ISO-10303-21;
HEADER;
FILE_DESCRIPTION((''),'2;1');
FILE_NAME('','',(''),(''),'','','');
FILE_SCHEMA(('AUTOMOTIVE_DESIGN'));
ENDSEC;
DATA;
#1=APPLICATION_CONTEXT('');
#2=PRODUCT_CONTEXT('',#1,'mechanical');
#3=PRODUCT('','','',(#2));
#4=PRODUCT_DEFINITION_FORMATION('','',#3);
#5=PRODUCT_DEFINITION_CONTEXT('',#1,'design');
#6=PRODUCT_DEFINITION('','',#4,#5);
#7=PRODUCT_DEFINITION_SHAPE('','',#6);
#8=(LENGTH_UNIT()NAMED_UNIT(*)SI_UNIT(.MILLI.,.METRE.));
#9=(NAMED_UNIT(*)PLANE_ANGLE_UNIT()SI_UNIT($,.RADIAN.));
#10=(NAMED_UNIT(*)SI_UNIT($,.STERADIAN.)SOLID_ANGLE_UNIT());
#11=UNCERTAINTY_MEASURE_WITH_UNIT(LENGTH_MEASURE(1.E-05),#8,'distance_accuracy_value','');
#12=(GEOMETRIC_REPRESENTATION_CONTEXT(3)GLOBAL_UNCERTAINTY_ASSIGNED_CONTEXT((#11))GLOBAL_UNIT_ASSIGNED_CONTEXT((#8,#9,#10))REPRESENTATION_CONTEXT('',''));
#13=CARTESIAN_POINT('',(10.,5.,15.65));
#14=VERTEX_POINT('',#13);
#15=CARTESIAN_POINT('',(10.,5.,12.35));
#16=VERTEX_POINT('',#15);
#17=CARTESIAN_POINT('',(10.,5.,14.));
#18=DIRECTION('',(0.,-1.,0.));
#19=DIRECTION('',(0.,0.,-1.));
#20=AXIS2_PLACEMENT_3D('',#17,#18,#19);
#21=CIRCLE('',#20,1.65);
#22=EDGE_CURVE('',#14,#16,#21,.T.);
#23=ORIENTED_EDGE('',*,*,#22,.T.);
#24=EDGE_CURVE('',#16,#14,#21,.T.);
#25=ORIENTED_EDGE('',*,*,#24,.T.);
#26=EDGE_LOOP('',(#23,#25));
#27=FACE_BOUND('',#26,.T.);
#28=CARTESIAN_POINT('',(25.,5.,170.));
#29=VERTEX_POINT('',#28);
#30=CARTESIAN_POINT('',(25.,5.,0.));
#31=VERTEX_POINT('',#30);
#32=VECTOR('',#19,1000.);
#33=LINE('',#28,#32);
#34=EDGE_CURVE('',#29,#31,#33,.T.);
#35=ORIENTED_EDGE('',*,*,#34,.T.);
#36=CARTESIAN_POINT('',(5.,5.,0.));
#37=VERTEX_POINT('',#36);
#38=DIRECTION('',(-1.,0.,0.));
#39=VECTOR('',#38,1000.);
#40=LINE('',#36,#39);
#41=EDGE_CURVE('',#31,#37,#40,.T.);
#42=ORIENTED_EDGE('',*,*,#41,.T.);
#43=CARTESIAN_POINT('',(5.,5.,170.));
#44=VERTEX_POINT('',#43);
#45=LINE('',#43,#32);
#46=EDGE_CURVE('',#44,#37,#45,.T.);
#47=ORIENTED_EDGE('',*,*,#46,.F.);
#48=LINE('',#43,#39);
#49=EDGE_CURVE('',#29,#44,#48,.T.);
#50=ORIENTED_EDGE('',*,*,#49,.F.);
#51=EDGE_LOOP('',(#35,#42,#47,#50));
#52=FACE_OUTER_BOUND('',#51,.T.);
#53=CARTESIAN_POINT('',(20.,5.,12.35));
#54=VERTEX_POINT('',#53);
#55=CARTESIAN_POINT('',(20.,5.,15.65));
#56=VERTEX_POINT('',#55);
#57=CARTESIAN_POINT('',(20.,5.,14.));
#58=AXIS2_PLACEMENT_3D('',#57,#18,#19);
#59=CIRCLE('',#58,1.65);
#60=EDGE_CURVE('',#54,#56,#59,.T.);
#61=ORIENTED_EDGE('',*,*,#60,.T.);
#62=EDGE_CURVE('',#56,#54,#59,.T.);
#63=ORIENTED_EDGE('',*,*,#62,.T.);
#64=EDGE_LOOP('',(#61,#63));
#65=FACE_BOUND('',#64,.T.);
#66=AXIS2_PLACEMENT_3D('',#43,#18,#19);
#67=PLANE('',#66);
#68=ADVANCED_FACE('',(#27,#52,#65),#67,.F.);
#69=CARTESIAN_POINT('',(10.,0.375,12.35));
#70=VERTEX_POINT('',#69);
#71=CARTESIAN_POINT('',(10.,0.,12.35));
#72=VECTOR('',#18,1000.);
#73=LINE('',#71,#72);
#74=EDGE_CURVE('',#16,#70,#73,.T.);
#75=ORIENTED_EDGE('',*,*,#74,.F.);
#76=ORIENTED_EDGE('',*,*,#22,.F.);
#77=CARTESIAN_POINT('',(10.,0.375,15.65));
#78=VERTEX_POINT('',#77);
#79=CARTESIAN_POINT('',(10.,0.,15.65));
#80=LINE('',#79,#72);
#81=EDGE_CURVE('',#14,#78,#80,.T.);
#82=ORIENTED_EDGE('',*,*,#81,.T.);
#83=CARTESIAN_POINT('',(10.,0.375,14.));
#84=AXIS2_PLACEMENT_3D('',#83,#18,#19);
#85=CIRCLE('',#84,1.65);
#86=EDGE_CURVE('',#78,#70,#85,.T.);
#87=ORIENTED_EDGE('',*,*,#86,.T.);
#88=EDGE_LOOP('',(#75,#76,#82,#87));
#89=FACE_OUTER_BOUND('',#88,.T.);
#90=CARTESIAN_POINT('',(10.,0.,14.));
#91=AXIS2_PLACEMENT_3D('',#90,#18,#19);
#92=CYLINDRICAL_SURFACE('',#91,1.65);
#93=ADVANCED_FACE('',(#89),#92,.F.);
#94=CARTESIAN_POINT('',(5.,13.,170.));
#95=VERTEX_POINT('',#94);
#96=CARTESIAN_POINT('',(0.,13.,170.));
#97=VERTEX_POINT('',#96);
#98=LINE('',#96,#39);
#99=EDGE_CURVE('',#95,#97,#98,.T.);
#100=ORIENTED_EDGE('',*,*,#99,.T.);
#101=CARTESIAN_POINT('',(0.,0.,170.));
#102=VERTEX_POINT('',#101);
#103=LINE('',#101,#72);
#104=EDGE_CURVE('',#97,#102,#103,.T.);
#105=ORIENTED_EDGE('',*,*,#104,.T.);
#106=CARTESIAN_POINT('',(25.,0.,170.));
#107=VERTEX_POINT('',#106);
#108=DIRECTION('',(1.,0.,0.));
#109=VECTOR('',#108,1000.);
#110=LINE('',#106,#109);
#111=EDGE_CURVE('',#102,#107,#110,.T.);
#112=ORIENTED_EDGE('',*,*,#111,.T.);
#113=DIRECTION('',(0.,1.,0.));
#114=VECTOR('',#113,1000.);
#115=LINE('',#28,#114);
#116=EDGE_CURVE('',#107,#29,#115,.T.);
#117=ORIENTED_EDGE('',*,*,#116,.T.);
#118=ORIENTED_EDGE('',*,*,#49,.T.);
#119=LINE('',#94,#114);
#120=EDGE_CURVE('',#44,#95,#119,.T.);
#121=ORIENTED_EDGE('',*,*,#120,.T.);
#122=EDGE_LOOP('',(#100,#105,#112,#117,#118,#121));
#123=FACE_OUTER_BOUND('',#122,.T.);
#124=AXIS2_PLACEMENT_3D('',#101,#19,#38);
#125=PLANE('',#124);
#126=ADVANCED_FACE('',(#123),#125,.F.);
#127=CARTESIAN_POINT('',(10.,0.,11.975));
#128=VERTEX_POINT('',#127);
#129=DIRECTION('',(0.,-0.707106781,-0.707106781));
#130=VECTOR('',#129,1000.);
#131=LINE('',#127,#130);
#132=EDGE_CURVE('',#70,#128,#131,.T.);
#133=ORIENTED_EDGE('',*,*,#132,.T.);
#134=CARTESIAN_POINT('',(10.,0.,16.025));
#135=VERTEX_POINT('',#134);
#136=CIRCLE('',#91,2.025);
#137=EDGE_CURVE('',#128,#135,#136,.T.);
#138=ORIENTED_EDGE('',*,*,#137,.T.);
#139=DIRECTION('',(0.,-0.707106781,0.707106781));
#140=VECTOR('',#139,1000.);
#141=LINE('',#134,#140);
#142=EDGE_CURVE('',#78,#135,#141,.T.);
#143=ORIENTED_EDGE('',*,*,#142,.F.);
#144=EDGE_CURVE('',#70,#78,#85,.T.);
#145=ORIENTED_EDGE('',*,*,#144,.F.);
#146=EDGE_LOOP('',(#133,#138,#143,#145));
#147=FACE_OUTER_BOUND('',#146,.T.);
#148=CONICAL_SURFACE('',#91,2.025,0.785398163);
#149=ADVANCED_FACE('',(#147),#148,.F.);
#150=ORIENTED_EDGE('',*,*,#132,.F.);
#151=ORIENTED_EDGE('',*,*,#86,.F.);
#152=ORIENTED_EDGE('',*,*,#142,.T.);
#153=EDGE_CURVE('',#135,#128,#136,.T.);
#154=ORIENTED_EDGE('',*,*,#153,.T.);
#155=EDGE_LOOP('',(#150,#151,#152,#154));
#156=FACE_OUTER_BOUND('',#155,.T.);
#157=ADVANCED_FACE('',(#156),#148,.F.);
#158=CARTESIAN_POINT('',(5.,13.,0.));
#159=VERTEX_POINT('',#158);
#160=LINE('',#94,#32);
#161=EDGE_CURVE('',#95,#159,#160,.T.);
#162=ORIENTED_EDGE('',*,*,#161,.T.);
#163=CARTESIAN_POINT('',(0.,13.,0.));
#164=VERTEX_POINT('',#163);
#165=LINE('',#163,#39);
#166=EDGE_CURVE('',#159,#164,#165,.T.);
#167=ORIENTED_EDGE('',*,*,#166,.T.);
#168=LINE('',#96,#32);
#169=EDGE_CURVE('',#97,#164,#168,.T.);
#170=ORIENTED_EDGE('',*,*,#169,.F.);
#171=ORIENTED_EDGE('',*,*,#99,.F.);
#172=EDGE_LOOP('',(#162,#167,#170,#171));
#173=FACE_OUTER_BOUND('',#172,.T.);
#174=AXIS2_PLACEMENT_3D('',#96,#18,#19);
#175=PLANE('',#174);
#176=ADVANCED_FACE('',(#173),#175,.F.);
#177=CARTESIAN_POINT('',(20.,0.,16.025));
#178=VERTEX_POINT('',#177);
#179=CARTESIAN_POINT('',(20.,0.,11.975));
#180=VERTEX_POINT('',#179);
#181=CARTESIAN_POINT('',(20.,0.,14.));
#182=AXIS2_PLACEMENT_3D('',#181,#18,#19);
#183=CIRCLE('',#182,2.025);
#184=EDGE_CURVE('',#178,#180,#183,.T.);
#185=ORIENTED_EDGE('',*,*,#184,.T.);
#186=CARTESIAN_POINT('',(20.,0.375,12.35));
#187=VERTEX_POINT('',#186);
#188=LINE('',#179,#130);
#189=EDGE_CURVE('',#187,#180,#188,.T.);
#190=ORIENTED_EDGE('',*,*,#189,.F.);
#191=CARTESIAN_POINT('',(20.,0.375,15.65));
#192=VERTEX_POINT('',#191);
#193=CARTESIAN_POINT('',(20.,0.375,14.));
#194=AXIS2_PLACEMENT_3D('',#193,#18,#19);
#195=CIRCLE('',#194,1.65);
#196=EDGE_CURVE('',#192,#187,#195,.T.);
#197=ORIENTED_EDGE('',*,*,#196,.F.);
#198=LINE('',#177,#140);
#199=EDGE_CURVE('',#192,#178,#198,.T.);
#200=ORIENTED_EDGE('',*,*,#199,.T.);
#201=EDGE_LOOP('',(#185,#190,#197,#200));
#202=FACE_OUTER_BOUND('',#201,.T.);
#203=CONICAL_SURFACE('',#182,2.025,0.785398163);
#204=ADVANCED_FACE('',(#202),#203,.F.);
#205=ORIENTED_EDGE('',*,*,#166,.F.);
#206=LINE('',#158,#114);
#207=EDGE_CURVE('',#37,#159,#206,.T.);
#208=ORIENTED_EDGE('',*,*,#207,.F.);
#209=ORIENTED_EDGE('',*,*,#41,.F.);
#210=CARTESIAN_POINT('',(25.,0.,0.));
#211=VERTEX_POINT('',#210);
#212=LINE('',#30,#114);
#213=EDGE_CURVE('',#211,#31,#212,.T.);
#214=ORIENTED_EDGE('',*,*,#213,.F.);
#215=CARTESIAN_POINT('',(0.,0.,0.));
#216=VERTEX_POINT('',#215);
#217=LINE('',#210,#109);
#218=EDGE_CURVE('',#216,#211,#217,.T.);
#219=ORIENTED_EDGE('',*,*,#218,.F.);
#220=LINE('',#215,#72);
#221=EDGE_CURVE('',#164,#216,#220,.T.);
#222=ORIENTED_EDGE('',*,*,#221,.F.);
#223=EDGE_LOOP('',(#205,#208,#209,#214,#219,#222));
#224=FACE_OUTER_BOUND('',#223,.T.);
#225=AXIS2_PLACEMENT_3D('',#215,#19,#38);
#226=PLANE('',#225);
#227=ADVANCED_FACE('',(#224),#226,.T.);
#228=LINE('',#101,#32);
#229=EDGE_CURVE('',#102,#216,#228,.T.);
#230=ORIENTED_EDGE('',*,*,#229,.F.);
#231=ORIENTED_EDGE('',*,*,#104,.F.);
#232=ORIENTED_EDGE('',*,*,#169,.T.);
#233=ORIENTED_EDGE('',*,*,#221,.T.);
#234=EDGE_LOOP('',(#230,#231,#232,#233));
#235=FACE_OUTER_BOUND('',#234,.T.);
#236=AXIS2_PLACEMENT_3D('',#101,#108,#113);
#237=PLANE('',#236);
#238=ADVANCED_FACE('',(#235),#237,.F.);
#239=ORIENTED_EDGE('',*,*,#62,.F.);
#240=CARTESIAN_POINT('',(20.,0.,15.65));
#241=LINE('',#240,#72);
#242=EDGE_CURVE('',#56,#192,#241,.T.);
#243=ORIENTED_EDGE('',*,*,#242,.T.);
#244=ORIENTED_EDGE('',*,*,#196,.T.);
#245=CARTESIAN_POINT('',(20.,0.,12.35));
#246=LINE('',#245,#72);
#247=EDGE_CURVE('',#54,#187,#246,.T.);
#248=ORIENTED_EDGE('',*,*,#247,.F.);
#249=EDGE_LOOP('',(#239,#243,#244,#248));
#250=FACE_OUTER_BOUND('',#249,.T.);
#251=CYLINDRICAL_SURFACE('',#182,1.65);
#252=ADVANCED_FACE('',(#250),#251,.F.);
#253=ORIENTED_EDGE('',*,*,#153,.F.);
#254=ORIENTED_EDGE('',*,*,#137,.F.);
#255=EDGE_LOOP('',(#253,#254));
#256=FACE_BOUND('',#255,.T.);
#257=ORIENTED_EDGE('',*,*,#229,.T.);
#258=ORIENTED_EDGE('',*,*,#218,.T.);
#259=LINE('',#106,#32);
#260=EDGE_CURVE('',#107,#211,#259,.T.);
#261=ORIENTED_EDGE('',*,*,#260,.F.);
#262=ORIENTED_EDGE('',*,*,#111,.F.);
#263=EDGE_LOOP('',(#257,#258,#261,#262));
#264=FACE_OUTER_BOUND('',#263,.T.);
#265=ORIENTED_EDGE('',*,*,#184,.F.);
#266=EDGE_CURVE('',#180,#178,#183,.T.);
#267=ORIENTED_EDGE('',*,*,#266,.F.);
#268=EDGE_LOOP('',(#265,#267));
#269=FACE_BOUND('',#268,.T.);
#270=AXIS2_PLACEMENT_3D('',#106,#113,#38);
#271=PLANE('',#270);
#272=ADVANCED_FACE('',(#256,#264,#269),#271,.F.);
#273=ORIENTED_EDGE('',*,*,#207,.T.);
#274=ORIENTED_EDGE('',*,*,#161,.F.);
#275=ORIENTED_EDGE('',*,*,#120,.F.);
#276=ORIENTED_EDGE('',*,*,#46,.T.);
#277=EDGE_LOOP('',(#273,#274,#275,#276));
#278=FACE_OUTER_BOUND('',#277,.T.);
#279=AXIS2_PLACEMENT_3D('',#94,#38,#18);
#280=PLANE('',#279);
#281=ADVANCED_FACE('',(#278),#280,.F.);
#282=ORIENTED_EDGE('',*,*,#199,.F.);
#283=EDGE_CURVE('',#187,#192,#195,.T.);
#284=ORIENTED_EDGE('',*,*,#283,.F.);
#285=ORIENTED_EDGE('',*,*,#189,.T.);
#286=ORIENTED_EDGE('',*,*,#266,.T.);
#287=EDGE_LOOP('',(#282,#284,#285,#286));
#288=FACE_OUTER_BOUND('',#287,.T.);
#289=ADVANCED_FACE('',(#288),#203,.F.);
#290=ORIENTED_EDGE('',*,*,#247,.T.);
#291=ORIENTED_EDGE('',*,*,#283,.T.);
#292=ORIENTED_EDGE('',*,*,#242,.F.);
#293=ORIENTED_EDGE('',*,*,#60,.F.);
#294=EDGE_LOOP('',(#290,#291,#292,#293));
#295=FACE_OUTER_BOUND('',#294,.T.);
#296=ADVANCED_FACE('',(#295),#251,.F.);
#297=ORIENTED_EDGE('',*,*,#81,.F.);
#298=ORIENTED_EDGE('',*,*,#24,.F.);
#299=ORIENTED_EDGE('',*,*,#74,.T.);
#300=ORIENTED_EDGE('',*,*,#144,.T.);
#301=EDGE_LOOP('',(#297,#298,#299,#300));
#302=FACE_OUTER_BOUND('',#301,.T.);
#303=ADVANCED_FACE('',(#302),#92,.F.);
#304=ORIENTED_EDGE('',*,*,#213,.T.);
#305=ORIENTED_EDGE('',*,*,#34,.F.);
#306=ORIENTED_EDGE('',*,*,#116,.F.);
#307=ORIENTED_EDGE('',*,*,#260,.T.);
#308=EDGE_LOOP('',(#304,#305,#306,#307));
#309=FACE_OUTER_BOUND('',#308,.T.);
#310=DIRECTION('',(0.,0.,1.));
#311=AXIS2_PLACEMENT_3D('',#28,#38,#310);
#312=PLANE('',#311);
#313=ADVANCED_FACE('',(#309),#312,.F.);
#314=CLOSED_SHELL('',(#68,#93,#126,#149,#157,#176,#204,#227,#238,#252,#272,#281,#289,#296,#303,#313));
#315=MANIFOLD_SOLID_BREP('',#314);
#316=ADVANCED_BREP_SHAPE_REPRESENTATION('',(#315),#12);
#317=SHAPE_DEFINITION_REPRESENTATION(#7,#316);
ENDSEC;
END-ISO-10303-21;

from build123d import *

# Parameters (mm, degrees)
EXTRUDE_1_DEPTH              = 170
HOLE_WIZARD_M4_1_D           = 3.3
HOLE_WIZARD_M4_1_CSINK_D     = 4.05
HOLE_WIZARD_M4_1_CSINK_ANGLE = 90


with BuildPart() as part:
    # 草图1 → 凸台-拉伸1 (new body)
    with BuildSketch(Plane.XY):
        Polygon((0, 0), (0, 13), (5, 13), (5, 5), (25, 5), (25, 0), align=None)
    extrude(amount=EXTRUDE_1_DEPTH)

    # M4 螺纹孔1 (through all)
    with Locations(Plane(origin=(10, 0, 14), x_dir=(-1, 0, 0), z_dir=(0, -1, 0))):
        with Locations((0, 0), (-10, 0)):
            CounterSinkHole(HOLE_WIZARD_M4_1_D / 2, HOLE_WIZARD_M4_1_CSINK_D / 2, counter_sink_angle=HOLE_WIZARD_M4_1_CSINK_ANGLE)


solid = part.part
